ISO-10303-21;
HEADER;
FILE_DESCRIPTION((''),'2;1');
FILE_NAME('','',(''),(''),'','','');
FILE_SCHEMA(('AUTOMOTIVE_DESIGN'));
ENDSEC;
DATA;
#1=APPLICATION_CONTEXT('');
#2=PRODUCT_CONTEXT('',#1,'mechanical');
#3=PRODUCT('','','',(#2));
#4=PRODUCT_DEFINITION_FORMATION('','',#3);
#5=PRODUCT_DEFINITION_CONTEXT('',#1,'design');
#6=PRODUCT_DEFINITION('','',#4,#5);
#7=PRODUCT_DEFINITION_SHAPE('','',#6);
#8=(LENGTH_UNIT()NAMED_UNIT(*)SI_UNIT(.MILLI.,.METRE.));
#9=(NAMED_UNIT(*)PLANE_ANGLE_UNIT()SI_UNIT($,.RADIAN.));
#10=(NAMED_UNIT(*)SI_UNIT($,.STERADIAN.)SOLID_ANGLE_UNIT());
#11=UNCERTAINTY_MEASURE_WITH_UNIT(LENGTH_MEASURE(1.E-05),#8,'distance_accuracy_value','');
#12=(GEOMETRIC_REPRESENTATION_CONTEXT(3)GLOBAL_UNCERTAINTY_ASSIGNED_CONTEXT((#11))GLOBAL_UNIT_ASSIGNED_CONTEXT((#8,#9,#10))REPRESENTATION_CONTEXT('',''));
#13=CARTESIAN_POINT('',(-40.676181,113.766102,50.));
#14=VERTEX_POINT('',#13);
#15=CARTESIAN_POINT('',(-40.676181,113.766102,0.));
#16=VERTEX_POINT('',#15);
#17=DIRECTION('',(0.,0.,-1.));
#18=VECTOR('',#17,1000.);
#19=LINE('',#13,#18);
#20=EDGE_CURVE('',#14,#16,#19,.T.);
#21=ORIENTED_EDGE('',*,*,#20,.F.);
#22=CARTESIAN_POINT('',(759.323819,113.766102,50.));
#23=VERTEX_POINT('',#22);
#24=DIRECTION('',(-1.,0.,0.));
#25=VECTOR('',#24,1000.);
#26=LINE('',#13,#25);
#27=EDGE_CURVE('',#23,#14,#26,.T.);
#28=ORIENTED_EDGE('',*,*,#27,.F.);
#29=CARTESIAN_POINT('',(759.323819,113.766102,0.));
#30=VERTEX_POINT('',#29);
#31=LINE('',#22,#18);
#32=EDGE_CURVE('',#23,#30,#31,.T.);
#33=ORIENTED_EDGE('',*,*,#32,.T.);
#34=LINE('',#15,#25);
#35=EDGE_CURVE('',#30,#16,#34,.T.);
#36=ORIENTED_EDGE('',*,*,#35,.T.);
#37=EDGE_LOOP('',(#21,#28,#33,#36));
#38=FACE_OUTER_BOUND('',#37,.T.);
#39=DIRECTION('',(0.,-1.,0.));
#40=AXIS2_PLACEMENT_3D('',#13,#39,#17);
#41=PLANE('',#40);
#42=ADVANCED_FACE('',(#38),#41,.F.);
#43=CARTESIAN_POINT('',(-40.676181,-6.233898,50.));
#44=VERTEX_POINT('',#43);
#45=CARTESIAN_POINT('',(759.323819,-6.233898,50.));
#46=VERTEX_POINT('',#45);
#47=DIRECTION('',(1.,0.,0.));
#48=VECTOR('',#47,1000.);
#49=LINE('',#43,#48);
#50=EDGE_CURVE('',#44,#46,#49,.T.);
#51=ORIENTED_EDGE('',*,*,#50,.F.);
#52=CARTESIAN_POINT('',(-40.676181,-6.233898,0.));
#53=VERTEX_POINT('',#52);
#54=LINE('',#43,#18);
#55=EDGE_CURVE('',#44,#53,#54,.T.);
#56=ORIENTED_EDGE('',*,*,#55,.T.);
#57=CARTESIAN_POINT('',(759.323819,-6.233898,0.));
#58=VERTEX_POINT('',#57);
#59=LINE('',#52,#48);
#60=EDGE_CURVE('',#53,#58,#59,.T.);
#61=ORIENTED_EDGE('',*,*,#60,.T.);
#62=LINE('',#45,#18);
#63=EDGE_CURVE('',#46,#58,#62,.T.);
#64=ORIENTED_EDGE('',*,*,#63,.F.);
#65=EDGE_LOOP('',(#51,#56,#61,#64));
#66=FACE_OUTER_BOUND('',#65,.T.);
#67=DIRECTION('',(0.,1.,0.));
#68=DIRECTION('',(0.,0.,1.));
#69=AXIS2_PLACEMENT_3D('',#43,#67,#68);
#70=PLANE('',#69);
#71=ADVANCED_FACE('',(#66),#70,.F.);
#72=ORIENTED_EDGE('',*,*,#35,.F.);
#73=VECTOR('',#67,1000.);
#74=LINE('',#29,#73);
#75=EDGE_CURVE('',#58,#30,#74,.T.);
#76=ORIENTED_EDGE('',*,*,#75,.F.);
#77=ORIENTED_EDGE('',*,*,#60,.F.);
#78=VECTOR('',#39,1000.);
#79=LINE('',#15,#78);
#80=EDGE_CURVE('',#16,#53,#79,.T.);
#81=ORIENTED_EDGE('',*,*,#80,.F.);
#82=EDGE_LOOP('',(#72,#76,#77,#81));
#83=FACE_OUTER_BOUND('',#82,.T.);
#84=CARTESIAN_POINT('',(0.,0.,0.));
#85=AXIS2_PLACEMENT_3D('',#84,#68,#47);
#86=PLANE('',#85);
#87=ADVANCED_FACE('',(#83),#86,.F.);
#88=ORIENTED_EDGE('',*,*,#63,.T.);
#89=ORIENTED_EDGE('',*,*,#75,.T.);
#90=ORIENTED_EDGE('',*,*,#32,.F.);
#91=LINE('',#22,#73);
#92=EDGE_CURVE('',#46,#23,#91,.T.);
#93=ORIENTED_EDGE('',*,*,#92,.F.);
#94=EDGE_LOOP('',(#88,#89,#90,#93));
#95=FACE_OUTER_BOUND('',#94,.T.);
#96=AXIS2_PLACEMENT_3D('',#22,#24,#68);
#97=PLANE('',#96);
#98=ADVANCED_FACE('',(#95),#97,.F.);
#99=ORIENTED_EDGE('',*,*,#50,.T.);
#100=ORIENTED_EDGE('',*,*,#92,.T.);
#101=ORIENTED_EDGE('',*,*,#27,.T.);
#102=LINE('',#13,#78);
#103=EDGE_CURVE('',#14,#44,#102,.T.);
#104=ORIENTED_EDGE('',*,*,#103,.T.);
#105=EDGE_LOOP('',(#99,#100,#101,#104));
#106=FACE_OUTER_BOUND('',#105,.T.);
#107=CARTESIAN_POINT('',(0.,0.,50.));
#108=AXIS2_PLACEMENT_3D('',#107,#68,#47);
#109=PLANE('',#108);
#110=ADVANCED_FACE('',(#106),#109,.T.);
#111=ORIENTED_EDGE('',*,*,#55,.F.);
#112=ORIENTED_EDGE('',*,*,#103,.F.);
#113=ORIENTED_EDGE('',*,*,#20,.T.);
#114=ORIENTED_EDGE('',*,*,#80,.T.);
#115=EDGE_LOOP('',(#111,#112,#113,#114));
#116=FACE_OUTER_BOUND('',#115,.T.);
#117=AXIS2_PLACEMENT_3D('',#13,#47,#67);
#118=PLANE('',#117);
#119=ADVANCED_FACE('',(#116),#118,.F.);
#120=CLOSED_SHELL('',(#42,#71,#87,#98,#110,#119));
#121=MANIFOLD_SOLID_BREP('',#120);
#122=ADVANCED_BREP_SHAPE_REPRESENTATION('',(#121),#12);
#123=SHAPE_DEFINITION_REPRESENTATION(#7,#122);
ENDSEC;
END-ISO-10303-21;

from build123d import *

# Parameters (mm, degrees)
SKETCH_1_W      = 800
SKETCH_1_H      = 120
EXTRUDE_1_DEPTH = 50


with BuildPart() as part:
    # 草图1 → 凸台-拉伸1 (new body)
    with BuildSketch(Plane.XY):
        with Locations((359.323818564, 53.766102462)):
            Rectangle(SKETCH_1_W, SKETCH_1_H)
    extrude(amount=EXTRUDE_1_DEPTH)


solid = part.part
